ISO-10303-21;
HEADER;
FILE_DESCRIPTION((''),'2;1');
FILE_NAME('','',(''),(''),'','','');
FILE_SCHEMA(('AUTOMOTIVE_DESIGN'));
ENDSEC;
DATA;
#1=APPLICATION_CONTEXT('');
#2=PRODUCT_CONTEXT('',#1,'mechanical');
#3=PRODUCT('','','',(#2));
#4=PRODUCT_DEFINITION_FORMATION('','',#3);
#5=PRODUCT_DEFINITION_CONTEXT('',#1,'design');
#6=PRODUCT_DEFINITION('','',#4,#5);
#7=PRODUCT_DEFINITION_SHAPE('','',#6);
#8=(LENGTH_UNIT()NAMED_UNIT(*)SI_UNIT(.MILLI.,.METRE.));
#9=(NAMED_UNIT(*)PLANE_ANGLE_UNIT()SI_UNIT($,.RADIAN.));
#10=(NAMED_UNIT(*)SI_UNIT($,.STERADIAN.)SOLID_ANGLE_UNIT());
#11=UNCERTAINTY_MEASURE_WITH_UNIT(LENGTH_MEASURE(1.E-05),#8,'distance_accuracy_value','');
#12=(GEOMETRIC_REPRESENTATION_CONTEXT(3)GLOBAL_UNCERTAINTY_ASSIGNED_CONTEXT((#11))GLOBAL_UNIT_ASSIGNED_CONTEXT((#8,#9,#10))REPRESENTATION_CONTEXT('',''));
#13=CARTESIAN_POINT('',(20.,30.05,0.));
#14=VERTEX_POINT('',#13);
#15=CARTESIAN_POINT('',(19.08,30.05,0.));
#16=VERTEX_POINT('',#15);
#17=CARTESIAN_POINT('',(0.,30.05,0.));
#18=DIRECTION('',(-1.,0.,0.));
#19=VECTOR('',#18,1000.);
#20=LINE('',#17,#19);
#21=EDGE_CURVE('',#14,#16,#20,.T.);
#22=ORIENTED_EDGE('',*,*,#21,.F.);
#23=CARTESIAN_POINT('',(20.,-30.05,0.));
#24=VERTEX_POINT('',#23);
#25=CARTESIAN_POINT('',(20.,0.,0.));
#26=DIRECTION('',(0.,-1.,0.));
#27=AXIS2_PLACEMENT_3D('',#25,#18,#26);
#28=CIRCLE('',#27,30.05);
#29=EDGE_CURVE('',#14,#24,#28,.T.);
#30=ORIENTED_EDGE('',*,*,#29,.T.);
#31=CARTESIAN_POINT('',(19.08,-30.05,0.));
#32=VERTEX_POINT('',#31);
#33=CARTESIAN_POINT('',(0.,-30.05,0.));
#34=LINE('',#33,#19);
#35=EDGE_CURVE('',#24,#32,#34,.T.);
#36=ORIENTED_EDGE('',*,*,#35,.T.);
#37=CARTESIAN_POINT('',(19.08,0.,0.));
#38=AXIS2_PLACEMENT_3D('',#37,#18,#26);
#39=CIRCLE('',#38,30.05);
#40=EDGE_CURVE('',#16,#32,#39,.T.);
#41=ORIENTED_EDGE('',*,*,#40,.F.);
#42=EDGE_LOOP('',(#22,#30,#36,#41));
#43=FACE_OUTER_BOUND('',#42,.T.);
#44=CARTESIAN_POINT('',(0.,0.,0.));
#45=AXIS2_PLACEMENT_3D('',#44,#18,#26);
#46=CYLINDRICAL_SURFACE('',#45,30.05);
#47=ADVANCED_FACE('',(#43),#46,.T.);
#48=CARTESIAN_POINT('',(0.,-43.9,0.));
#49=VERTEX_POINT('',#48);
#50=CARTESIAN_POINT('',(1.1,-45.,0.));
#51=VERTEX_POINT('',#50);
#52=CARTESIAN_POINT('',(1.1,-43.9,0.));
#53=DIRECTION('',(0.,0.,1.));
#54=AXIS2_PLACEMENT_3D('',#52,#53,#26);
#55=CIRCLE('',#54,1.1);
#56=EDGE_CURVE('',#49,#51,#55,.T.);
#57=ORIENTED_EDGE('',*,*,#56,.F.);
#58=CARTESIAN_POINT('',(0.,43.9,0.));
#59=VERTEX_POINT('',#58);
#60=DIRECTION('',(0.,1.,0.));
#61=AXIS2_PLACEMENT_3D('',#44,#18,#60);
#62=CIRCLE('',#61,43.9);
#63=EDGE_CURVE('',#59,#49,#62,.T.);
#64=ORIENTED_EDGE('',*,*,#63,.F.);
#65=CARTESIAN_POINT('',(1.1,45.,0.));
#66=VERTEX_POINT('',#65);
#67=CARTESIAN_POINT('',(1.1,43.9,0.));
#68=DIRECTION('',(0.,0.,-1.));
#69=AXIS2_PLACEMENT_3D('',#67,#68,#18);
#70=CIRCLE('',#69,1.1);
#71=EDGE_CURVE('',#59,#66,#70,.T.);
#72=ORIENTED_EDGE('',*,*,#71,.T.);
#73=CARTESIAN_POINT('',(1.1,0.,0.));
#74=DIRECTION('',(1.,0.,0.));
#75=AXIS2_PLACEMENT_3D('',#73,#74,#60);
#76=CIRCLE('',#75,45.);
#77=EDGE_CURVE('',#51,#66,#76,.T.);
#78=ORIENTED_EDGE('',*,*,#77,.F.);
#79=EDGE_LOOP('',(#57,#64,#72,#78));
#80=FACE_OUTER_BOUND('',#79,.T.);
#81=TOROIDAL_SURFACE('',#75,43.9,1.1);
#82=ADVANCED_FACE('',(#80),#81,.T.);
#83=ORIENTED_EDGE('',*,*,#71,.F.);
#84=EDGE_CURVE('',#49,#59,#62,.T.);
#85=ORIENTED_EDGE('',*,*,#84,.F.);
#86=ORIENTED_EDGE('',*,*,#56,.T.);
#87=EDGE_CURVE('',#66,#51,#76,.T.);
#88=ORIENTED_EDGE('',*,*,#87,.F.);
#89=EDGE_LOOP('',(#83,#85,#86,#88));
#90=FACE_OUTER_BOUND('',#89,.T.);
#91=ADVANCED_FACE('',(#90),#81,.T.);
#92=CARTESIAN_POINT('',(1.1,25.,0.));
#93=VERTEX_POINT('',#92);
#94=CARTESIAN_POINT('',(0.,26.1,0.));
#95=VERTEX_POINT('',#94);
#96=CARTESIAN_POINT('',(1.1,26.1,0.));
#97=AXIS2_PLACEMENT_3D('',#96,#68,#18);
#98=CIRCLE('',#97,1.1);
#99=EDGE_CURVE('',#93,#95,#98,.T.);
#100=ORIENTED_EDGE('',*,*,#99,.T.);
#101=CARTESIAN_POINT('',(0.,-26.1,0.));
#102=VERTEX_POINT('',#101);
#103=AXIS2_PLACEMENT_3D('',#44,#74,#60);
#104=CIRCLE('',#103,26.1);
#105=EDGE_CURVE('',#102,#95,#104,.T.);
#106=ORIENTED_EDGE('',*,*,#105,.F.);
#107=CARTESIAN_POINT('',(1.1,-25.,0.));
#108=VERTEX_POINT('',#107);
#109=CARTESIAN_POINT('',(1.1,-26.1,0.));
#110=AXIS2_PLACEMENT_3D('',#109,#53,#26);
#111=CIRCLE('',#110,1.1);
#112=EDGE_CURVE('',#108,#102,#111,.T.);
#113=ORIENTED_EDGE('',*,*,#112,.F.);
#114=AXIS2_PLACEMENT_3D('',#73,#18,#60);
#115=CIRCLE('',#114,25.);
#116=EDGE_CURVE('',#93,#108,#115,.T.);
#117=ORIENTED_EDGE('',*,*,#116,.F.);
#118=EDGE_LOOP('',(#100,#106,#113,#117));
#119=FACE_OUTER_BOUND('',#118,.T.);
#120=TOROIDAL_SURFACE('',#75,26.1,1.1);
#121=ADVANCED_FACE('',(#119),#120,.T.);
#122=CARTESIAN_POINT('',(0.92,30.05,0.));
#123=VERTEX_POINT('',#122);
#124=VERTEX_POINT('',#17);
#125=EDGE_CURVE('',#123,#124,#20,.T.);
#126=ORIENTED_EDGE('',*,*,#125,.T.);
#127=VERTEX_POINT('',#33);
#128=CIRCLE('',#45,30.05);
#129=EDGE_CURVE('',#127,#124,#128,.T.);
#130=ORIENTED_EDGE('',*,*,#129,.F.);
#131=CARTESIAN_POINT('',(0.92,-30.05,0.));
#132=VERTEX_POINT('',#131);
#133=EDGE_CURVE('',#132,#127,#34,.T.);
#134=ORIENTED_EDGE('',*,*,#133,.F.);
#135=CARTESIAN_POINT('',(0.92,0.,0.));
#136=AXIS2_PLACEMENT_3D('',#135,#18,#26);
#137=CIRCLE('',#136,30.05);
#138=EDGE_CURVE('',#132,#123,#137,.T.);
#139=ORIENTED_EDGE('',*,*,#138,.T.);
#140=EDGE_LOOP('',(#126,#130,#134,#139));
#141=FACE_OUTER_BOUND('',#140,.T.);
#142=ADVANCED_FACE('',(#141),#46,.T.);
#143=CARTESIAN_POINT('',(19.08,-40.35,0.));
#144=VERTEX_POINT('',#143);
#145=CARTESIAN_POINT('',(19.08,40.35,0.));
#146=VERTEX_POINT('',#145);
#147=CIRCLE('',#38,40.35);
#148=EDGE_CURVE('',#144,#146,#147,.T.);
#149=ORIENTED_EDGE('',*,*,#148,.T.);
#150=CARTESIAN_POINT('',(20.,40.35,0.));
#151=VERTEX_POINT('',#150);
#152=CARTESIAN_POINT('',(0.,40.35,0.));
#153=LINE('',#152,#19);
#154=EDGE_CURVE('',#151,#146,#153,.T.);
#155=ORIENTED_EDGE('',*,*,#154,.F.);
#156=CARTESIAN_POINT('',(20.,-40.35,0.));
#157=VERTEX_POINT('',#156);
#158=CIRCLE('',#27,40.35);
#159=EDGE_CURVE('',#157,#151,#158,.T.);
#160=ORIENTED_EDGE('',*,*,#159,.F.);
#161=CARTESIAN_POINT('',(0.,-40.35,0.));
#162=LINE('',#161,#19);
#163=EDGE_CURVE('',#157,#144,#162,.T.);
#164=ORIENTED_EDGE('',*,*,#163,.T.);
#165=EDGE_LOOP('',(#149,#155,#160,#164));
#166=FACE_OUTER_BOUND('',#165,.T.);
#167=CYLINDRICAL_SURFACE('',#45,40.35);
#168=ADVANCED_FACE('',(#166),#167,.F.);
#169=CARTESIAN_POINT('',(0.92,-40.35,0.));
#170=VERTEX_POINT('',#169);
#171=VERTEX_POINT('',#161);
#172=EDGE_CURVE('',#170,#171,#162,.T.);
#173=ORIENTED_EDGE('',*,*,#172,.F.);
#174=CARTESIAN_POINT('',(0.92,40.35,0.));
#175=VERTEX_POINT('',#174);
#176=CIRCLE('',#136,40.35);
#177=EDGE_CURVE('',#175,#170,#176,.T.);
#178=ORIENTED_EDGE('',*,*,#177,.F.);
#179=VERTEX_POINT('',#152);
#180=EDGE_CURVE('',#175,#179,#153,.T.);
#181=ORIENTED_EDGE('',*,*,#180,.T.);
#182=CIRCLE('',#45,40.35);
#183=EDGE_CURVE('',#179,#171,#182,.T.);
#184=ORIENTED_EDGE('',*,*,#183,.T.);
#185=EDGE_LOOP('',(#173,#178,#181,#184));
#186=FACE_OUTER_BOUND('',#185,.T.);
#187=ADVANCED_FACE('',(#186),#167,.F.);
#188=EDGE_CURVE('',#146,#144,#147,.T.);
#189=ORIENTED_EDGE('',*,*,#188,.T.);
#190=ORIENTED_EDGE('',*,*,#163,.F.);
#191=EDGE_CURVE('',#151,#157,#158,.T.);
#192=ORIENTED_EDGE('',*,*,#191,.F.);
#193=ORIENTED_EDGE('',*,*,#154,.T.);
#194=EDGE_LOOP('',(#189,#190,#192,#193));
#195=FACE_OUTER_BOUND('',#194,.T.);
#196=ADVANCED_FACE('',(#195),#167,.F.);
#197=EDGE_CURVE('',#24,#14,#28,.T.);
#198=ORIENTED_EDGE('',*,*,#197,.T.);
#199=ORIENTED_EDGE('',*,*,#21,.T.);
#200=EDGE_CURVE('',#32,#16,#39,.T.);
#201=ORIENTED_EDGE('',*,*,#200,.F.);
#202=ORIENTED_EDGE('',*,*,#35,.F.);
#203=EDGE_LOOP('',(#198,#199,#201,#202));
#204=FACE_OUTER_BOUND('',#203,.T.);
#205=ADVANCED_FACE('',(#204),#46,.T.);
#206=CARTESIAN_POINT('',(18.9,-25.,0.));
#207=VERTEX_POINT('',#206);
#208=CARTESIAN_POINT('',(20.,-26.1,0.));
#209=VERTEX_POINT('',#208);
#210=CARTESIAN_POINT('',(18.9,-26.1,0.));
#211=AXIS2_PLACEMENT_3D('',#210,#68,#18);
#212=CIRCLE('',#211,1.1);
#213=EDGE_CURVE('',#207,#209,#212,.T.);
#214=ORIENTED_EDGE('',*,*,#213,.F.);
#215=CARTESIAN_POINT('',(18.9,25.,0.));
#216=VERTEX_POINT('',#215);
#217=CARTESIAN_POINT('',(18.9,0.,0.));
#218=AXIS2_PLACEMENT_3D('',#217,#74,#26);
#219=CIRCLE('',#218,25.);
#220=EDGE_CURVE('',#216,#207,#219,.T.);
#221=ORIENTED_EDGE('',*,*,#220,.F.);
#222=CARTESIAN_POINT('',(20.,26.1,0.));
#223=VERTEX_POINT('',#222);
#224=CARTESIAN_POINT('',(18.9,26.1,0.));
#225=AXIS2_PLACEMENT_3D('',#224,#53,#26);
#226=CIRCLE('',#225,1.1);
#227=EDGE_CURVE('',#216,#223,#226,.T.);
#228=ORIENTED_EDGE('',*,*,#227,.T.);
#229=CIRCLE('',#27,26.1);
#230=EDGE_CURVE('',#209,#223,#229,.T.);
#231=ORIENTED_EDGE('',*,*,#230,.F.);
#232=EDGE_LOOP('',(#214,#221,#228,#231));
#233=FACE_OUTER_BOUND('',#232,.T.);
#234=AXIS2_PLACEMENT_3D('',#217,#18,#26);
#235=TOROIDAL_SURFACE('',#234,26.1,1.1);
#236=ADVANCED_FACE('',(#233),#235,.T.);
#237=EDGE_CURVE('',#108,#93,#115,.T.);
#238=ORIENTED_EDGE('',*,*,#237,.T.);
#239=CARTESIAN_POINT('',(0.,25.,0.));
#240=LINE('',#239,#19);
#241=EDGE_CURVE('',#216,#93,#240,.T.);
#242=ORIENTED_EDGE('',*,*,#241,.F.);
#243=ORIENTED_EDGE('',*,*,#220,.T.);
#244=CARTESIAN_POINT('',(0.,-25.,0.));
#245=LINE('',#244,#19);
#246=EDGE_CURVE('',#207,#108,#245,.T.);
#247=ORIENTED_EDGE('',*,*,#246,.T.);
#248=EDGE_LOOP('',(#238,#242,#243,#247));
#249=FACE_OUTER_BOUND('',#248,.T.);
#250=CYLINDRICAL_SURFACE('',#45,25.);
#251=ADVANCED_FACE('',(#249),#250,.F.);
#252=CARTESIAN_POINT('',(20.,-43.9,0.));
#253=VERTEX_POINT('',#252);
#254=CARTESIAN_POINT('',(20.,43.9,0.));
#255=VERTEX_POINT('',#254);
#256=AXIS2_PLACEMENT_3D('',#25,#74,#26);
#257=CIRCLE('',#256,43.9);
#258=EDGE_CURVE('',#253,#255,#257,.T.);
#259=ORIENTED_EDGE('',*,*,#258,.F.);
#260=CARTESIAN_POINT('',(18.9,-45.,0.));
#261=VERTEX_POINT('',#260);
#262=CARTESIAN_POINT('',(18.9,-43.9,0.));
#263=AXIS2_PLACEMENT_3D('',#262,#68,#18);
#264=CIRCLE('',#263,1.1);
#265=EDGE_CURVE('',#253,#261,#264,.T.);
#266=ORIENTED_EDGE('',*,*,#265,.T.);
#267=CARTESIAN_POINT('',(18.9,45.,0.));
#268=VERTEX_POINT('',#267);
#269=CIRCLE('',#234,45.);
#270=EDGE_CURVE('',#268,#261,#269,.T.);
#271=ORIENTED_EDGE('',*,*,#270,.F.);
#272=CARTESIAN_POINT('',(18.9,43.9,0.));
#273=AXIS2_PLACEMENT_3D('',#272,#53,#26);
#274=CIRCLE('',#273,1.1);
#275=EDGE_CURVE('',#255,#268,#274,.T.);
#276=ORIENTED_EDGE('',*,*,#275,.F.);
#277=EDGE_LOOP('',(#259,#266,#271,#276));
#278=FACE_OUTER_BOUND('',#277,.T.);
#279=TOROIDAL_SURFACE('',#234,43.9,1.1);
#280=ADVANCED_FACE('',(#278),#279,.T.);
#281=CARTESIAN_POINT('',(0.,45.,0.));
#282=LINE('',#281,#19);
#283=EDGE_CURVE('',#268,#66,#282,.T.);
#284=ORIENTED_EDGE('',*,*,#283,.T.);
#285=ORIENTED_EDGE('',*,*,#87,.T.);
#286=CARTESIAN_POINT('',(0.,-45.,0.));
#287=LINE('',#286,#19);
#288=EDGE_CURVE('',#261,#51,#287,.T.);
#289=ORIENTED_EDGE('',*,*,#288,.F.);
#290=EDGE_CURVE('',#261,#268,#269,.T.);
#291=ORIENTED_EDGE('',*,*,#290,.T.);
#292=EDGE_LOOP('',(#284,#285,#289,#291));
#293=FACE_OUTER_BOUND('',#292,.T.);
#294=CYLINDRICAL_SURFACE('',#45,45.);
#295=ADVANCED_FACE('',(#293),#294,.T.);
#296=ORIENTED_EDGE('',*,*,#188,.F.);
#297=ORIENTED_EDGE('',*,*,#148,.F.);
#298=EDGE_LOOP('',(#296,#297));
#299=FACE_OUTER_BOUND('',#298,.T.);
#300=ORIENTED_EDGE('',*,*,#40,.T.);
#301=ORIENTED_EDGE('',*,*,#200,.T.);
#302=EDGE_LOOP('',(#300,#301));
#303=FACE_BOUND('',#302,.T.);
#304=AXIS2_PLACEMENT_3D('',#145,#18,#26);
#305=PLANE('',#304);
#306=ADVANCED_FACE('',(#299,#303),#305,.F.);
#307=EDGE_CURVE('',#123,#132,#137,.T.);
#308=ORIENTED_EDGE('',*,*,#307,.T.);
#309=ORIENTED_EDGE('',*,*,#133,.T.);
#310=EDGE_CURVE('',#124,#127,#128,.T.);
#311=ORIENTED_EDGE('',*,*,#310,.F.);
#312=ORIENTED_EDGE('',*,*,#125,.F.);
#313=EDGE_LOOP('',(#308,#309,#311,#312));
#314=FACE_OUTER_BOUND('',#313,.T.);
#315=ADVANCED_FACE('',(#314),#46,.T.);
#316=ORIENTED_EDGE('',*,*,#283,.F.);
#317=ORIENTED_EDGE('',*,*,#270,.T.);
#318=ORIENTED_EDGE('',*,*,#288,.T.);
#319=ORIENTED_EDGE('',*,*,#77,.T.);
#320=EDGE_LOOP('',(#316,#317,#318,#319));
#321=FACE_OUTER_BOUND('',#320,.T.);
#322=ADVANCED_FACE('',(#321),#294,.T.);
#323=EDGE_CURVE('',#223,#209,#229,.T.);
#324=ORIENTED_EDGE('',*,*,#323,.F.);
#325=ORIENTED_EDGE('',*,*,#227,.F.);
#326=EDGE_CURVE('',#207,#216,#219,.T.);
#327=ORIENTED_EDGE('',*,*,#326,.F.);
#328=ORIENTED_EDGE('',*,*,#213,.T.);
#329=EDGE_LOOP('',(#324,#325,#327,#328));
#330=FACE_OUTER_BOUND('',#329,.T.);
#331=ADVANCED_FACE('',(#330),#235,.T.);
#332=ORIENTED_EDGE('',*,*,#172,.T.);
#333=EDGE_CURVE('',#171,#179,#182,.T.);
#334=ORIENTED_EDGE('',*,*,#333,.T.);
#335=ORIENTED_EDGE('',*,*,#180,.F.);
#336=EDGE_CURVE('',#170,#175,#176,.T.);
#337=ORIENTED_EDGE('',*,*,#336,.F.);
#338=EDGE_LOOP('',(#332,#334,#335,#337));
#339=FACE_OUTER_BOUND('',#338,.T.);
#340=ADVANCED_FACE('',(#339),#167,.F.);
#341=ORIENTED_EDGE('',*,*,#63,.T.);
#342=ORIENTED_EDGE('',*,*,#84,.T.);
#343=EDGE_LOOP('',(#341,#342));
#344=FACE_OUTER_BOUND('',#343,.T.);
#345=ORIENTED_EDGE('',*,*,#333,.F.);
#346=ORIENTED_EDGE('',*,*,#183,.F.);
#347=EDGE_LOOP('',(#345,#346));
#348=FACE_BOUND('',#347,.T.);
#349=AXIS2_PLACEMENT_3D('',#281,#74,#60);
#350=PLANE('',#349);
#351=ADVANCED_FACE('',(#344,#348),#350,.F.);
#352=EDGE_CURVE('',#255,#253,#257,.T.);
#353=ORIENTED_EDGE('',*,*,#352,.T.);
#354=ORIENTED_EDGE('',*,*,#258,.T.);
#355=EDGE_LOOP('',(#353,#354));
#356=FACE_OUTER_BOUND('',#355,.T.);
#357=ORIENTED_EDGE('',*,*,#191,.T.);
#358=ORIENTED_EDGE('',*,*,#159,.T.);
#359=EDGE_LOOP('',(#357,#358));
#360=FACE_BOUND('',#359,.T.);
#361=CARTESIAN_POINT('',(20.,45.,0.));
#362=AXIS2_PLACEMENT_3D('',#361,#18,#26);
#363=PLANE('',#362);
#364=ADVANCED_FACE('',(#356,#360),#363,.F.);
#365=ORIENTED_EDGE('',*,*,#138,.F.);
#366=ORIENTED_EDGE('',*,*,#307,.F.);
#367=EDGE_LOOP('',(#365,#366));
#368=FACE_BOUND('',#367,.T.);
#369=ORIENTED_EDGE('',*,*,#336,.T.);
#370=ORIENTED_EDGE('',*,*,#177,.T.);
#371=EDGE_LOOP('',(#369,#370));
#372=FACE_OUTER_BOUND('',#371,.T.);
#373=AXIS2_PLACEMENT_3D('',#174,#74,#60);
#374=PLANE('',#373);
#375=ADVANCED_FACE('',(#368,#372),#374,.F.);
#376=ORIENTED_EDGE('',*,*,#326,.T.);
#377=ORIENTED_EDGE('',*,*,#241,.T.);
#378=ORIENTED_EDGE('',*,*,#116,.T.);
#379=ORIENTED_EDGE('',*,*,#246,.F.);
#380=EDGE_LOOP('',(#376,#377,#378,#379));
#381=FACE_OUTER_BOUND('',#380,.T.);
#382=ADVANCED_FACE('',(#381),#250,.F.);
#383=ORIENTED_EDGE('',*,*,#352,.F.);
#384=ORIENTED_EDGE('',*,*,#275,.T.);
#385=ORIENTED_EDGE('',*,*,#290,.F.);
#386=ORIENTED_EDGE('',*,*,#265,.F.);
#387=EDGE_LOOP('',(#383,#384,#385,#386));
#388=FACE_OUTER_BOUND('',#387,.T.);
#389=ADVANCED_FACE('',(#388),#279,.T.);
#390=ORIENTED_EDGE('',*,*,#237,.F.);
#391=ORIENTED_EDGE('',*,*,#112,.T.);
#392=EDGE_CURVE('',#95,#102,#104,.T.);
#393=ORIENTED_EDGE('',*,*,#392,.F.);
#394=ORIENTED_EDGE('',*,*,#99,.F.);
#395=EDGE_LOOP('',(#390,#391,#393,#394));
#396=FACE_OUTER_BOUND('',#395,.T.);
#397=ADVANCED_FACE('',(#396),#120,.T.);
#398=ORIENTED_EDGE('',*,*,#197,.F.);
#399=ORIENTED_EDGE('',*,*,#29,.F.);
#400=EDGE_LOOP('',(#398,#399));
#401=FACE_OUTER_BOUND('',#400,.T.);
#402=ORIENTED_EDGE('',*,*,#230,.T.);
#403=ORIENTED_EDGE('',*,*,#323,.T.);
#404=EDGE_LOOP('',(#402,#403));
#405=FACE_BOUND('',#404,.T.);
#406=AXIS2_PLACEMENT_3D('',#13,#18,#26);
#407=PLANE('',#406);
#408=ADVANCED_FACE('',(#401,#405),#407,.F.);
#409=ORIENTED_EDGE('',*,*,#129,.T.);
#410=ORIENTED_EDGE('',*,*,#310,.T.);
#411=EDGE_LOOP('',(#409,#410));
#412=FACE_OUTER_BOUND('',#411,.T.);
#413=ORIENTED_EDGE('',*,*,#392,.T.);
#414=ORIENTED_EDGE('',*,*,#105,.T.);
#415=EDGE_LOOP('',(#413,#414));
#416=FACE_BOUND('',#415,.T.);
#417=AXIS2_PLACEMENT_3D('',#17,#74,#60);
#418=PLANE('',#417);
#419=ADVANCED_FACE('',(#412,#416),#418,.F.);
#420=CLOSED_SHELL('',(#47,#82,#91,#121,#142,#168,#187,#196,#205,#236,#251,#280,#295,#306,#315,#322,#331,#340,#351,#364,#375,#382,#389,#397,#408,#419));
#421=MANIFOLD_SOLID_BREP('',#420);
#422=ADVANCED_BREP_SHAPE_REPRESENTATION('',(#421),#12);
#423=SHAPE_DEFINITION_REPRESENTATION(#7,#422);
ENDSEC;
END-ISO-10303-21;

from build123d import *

# Parameters (mm, degrees)
FILLET1_R = 1.1
FILLET2_R = 1.1


with BuildPart() as part:
    # Sketch1 → Revolve1 (revolve)
    with BuildSketch(Plane.XY, mode=Mode.PRIVATE) as revolve1_sk:
        Polygon((0, 25), (20, 25), (20, 30.05), (19.08, 30.05), (19.08, 40.35), (20, 40.35), (20, 45), (0, 45), (0, 40.35), (0.92, 40.35), (0.92, 30.05), (0, 30.05), align=None)
    revolve(revolve1_sk.sketch.rotate(Axis((0, 0, 0), (1, 0, 0)), 180), axis=Axis((0, 0, 0), (1, 0, 0)))

    # Fillet1
    fillet1_edges = [part.edges().sort_by_distance(p)[0] for p in [
        (0, 45, 0),
        (20, 45, 0),
    ]]
    fillet(fillet1_edges, radius=FILLET1_R)

    # Fillet2
    fillet2_edges = [part.edges().sort_by_distance(p)[0] for p in [
        (20, 25, 0),
        (0, 25, 0),
    ]]
    fillet(fillet2_edges, radius=FILLET2_R)


solid = part.part
